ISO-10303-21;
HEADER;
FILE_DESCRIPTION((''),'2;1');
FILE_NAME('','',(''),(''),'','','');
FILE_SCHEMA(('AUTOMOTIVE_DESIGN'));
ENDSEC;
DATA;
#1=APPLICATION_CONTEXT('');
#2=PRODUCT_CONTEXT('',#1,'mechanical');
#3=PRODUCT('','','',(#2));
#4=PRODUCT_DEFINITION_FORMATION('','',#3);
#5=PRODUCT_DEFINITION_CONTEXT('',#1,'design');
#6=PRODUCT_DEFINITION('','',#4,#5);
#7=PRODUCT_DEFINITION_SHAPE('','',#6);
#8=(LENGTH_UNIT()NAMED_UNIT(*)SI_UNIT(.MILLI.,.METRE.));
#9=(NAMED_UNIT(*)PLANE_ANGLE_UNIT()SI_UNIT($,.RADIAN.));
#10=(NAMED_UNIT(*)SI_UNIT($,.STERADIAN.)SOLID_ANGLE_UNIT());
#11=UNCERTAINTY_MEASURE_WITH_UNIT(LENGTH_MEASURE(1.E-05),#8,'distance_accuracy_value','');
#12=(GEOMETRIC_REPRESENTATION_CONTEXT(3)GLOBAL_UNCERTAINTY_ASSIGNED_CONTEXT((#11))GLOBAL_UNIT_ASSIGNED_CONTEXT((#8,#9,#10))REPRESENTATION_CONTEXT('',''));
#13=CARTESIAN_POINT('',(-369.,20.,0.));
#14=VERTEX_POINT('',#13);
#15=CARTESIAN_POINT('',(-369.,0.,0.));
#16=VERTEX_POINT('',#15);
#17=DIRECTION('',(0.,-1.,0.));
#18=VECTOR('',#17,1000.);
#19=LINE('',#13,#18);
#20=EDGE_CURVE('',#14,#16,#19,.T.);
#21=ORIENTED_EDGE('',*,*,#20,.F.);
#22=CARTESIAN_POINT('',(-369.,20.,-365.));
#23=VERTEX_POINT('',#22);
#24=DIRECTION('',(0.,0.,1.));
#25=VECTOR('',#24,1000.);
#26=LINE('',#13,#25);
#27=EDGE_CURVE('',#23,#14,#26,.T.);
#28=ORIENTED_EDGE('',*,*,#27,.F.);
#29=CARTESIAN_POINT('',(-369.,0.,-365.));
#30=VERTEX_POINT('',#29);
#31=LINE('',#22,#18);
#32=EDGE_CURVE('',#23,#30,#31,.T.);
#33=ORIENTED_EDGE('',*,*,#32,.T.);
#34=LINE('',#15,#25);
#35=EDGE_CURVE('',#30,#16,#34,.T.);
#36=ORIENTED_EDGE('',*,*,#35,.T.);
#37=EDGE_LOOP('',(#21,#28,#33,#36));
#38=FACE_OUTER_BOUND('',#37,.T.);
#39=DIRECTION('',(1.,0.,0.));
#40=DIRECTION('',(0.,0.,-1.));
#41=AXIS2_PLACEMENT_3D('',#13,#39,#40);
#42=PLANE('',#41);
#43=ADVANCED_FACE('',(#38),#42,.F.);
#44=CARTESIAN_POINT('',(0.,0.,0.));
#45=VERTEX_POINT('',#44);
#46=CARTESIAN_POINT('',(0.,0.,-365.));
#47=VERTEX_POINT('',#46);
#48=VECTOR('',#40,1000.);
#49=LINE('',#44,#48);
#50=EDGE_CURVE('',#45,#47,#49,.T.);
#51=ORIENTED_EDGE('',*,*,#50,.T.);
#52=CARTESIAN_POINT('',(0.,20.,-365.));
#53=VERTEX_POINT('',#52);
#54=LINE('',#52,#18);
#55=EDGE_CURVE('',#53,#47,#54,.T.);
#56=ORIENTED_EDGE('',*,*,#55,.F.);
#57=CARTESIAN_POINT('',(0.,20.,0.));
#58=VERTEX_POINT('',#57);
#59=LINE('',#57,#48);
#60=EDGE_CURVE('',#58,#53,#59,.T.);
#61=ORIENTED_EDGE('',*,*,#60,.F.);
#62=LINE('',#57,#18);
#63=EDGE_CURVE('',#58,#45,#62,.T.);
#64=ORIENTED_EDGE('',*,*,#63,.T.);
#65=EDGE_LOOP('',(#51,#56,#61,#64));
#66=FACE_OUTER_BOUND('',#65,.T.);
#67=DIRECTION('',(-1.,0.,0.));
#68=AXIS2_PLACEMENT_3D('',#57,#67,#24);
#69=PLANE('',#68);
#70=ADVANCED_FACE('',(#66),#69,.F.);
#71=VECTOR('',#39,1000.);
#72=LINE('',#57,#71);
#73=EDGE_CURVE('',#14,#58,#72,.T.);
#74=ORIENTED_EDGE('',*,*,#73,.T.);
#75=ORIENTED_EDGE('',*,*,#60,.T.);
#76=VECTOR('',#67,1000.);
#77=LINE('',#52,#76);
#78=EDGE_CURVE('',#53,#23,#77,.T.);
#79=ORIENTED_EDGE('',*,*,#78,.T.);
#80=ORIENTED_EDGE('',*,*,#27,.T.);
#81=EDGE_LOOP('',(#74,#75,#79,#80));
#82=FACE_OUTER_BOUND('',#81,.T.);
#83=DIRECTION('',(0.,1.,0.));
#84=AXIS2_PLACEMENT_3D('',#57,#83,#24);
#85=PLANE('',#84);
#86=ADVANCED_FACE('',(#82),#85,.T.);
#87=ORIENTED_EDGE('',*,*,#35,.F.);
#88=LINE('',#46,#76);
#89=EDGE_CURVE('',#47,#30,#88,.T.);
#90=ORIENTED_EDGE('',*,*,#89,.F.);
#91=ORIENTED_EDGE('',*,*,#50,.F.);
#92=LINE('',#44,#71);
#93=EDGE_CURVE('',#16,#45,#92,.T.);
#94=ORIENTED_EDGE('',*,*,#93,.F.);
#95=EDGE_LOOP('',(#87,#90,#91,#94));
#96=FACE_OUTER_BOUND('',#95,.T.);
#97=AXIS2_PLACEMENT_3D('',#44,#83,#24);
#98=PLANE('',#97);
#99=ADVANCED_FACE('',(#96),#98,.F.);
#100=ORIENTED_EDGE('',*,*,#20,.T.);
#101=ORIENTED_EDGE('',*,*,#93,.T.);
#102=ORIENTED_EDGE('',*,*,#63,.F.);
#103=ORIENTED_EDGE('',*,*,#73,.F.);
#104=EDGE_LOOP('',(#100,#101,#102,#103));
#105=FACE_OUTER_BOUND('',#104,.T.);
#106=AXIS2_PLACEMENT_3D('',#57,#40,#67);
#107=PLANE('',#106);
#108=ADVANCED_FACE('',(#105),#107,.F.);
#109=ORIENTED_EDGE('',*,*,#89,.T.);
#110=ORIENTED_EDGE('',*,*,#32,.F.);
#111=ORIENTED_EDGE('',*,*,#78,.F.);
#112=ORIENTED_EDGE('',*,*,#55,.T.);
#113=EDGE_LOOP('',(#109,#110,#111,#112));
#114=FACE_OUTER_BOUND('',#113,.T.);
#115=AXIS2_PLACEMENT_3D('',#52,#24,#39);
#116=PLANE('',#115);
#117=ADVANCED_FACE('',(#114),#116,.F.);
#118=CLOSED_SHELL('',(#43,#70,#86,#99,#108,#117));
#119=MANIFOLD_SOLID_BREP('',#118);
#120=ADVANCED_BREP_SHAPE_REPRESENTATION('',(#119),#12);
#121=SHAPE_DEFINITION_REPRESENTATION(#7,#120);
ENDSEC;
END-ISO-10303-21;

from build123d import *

# Parameters (mm, degrees)
SKETCH1_W           = 369
SKETCH1_H           = 365
BOSS_EXTRUDE1_DEPTH = 20


with BuildPart() as part:
    # Sketch1 → Boss-Extrude1 (new body)
    with BuildSketch(Plane(origin=(0, 0, 0), x_dir=(1, 0, 0), z_dir=(0, 1, 0))):
        with Locations((-184.5, 182.5)):
            Rectangle(SKETCH1_W, SKETCH1_H)
    extrude(amount=BOSS_EXTRUDE1_DEPTH)


solid = part.part
